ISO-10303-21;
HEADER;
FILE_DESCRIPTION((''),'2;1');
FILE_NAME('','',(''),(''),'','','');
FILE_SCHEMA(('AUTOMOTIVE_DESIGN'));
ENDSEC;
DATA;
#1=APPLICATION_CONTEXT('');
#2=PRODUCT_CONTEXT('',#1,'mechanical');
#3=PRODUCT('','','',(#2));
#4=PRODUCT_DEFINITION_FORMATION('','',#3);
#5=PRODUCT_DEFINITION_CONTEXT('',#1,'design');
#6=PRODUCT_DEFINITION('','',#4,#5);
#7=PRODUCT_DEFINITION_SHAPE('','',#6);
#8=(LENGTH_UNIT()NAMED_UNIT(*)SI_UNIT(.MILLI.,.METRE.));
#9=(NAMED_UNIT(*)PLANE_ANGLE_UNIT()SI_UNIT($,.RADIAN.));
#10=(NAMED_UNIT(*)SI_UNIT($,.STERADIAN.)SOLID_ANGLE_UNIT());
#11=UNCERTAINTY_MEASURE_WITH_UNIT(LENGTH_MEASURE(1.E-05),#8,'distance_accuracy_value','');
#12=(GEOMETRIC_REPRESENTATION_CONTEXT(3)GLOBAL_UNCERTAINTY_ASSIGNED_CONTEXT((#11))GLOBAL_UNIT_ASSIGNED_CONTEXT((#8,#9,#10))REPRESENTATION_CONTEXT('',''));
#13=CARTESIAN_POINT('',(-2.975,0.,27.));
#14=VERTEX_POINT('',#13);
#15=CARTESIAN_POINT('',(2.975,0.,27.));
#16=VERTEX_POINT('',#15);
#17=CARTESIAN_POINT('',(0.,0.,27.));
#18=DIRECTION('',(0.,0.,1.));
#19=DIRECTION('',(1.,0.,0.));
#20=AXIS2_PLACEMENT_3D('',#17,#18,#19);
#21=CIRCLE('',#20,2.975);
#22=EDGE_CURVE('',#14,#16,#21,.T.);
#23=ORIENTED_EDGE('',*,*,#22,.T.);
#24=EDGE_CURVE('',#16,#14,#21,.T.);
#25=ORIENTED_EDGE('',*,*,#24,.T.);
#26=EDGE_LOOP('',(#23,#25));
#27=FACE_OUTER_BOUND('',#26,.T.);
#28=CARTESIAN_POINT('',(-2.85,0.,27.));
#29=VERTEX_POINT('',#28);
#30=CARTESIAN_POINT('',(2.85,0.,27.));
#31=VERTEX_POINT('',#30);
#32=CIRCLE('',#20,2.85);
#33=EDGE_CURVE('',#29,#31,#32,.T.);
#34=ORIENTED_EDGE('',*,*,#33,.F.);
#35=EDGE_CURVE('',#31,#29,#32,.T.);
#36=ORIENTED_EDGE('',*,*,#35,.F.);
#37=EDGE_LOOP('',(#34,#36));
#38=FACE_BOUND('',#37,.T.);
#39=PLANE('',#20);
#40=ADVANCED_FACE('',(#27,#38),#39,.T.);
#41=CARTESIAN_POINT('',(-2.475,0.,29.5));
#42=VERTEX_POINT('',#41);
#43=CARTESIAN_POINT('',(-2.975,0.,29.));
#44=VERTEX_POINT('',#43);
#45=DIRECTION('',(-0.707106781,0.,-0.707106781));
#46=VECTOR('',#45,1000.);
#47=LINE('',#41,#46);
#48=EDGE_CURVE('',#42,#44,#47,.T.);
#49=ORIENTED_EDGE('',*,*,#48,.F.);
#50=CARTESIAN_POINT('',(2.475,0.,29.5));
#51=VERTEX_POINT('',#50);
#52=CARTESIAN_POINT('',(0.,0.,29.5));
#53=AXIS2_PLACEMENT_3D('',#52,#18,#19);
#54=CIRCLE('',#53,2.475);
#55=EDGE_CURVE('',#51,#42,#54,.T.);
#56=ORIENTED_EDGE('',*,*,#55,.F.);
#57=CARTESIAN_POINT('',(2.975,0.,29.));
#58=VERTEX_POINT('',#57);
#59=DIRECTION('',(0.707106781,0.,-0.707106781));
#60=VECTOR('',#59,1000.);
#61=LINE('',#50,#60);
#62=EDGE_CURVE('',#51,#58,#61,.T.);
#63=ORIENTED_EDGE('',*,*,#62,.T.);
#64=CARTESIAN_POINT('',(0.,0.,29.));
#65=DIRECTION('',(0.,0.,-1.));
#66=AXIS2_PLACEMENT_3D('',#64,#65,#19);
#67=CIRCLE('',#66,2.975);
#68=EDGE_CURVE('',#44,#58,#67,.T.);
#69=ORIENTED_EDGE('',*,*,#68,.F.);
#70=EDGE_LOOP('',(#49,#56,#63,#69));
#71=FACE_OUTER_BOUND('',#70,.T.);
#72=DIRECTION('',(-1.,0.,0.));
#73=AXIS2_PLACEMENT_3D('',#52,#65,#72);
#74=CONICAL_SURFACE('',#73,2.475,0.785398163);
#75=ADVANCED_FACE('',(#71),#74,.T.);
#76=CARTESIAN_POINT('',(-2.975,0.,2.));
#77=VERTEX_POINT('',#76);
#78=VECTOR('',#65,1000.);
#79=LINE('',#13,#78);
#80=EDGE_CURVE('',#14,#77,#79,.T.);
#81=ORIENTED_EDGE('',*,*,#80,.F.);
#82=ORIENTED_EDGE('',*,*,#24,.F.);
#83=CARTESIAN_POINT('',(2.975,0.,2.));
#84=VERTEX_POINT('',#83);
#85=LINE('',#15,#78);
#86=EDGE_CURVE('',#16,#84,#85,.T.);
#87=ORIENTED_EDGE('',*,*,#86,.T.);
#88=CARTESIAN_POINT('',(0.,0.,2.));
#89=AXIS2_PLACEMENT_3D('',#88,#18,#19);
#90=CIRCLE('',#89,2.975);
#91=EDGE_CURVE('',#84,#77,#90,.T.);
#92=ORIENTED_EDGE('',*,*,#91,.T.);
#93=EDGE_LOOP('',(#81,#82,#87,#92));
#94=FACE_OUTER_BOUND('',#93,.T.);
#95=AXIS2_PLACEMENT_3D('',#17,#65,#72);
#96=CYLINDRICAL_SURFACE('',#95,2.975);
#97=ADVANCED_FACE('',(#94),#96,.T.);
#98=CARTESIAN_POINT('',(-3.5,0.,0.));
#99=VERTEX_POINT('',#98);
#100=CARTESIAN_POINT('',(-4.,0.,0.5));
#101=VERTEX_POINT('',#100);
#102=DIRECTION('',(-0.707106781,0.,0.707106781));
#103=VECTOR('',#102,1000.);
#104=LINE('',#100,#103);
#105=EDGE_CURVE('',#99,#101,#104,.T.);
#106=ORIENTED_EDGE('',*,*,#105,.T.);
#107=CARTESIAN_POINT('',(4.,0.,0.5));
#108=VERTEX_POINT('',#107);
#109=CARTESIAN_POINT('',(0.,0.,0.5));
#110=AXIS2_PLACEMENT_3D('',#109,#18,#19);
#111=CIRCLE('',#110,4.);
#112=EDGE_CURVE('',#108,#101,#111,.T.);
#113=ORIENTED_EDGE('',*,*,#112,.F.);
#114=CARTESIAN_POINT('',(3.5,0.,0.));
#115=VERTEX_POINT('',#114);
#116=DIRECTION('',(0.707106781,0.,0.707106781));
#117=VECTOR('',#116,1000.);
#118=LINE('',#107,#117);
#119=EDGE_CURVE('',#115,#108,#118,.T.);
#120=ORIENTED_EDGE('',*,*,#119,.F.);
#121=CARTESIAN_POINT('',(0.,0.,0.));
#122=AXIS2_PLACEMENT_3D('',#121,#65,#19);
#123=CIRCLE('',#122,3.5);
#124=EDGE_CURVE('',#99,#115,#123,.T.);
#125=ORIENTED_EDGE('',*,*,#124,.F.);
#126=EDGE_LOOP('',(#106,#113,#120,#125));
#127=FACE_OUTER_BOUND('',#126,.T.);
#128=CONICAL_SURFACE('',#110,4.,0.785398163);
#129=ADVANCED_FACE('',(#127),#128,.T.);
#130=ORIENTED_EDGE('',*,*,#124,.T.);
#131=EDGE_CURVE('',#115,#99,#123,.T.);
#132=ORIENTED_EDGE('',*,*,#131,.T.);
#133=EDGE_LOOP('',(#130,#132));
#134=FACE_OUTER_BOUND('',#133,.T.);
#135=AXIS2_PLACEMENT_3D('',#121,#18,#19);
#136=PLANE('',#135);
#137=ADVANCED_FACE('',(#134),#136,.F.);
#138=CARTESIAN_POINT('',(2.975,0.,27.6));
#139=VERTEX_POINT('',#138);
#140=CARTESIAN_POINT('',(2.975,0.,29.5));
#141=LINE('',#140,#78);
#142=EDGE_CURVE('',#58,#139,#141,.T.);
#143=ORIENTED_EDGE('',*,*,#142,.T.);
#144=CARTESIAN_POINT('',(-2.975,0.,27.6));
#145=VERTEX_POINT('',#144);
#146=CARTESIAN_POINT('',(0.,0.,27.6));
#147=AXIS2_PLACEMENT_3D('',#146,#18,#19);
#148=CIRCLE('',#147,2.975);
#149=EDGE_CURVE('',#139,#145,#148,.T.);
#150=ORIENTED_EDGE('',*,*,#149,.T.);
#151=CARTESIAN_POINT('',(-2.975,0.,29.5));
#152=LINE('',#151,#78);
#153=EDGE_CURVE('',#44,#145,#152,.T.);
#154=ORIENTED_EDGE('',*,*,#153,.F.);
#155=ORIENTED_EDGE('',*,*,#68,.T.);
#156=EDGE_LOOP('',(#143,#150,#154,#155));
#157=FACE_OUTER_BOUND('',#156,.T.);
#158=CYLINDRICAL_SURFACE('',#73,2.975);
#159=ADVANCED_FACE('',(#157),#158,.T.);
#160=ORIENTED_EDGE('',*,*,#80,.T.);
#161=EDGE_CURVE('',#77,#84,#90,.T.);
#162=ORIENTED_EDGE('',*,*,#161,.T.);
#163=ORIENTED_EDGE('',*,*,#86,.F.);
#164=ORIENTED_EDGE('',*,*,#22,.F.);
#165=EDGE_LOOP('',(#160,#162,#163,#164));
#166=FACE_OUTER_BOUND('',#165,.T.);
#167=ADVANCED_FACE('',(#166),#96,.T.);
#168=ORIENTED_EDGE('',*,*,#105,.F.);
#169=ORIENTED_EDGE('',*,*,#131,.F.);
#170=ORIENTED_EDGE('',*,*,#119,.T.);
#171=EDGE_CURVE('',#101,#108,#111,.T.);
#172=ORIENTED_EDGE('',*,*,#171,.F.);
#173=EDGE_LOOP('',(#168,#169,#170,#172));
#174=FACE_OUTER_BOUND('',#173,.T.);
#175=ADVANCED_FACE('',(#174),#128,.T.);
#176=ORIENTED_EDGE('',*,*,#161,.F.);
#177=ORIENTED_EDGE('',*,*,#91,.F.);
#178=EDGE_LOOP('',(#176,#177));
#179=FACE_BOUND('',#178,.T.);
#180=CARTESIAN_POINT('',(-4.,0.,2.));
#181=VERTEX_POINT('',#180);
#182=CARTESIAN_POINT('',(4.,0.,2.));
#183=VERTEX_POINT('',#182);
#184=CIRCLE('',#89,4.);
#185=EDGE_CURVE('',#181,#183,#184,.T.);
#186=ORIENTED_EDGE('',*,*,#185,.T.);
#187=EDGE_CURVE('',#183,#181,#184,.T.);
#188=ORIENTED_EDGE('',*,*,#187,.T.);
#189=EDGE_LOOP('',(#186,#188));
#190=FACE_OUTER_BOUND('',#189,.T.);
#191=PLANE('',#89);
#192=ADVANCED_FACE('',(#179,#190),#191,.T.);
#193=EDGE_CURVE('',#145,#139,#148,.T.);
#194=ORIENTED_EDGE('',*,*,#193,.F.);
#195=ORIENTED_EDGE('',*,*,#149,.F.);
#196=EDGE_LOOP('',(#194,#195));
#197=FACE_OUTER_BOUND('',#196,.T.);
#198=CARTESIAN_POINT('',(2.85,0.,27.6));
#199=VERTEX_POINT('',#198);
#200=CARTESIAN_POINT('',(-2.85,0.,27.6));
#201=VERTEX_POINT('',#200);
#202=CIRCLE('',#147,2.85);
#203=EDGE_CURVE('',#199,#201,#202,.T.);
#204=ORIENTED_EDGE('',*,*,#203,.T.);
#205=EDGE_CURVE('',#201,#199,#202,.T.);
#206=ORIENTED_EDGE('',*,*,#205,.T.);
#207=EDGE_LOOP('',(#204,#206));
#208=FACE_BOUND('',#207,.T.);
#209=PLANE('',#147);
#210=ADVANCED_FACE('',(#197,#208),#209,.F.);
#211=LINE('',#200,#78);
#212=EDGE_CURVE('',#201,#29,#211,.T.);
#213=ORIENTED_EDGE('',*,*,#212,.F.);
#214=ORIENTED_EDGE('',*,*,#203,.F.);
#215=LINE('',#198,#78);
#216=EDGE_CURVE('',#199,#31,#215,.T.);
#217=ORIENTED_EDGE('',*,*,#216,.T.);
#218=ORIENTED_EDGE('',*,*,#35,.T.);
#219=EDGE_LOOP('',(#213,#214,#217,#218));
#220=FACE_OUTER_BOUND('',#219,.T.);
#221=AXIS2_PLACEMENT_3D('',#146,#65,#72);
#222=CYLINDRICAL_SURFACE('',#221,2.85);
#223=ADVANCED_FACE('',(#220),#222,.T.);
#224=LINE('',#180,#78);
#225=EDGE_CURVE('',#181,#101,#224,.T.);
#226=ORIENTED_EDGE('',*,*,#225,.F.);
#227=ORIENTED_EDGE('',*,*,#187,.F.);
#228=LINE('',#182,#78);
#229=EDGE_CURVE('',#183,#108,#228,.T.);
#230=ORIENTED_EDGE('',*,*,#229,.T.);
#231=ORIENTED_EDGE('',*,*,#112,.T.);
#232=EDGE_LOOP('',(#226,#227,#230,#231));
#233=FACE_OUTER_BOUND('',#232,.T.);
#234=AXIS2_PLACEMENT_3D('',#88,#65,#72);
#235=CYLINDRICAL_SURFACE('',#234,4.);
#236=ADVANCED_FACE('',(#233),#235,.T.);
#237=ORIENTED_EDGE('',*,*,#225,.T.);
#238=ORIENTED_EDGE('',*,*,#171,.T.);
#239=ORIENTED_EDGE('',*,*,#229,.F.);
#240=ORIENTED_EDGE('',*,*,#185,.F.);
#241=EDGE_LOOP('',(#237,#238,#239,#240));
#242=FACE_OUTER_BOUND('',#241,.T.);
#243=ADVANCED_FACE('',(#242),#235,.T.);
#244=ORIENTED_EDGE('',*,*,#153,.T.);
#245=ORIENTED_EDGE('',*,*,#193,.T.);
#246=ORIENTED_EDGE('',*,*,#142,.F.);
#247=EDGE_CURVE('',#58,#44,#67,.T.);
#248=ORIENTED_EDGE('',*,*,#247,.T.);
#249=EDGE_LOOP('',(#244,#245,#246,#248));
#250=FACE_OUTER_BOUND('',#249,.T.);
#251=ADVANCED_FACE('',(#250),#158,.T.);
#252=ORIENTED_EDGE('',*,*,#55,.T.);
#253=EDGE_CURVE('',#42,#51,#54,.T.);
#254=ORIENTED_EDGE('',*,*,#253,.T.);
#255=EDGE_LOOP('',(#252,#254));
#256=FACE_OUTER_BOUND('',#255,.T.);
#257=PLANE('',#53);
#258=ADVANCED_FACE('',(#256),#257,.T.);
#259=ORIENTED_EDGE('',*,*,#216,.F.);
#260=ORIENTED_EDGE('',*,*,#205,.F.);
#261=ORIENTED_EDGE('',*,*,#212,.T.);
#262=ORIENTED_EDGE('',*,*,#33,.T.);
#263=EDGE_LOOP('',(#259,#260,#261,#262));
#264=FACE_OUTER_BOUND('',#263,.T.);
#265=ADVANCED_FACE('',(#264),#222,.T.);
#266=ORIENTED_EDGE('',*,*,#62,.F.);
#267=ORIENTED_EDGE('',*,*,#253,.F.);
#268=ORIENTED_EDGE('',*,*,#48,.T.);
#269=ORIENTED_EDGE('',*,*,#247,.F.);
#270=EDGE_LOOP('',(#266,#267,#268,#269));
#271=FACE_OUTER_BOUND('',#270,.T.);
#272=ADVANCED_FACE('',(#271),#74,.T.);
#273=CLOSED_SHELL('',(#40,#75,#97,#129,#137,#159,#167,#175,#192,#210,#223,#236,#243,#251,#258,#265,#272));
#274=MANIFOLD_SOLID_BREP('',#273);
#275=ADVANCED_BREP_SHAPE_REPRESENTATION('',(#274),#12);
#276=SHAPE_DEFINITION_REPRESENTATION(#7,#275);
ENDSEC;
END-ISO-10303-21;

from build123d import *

# Parameters (mm, degrees)
SKETCH1_R           = 4
BOSS_EXTRUDE1_DEPTH = 2
SKETCH3_R           = 2.975
BOSS_EXTRUDE2_DEPTH = 25
SKETCH4_R           = 2.85
BOSS_EXTRUDE3_DEPTH = 0.6
SKETCH5_R           = 2.975
BOSS_EXTRUDE4_DEPTH = 1.9
CHAMFER1_SIZE       = 0.5


with BuildPart() as part:
    # Sketch1 → Boss-Extrude1 (new body)
    with BuildSketch(Plane.XY):
        Circle(SKETCH1_R)
    extrude(amount=BOSS_EXTRUDE1_DEPTH)

    # Sketch3 → Boss-Extrude2 (add)
    with BuildSketch(Plane.XY.offset(2)):
        Circle(SKETCH3_R)
    extrude(amount=BOSS_EXTRUDE2_DEPTH)

    # Sketch4 → Boss-Extrude3 (add)
    with BuildSketch(Plane.XY.offset(27)):
        Circle(SKETCH4_R)
    extrude(amount=BOSS_EXTRUDE3_DEPTH)

    # Sketch5 → Boss-Extrude4 (add)
    with BuildSketch(Plane.XY.offset(27.6)):
        Circle(SKETCH5_R)
    extrude(amount=BOSS_EXTRUDE4_DEPTH)

    # Chamfer1
    chamfer1_edges = [part.edges().sort_by_distance(p)[0] for p in [
        (-2.975, 0, 29.5),
        (-4, 0, 0),
    ]]
    chamfer(chamfer1_edges, length=CHAMFER1_SIZE)


solid = part.part
